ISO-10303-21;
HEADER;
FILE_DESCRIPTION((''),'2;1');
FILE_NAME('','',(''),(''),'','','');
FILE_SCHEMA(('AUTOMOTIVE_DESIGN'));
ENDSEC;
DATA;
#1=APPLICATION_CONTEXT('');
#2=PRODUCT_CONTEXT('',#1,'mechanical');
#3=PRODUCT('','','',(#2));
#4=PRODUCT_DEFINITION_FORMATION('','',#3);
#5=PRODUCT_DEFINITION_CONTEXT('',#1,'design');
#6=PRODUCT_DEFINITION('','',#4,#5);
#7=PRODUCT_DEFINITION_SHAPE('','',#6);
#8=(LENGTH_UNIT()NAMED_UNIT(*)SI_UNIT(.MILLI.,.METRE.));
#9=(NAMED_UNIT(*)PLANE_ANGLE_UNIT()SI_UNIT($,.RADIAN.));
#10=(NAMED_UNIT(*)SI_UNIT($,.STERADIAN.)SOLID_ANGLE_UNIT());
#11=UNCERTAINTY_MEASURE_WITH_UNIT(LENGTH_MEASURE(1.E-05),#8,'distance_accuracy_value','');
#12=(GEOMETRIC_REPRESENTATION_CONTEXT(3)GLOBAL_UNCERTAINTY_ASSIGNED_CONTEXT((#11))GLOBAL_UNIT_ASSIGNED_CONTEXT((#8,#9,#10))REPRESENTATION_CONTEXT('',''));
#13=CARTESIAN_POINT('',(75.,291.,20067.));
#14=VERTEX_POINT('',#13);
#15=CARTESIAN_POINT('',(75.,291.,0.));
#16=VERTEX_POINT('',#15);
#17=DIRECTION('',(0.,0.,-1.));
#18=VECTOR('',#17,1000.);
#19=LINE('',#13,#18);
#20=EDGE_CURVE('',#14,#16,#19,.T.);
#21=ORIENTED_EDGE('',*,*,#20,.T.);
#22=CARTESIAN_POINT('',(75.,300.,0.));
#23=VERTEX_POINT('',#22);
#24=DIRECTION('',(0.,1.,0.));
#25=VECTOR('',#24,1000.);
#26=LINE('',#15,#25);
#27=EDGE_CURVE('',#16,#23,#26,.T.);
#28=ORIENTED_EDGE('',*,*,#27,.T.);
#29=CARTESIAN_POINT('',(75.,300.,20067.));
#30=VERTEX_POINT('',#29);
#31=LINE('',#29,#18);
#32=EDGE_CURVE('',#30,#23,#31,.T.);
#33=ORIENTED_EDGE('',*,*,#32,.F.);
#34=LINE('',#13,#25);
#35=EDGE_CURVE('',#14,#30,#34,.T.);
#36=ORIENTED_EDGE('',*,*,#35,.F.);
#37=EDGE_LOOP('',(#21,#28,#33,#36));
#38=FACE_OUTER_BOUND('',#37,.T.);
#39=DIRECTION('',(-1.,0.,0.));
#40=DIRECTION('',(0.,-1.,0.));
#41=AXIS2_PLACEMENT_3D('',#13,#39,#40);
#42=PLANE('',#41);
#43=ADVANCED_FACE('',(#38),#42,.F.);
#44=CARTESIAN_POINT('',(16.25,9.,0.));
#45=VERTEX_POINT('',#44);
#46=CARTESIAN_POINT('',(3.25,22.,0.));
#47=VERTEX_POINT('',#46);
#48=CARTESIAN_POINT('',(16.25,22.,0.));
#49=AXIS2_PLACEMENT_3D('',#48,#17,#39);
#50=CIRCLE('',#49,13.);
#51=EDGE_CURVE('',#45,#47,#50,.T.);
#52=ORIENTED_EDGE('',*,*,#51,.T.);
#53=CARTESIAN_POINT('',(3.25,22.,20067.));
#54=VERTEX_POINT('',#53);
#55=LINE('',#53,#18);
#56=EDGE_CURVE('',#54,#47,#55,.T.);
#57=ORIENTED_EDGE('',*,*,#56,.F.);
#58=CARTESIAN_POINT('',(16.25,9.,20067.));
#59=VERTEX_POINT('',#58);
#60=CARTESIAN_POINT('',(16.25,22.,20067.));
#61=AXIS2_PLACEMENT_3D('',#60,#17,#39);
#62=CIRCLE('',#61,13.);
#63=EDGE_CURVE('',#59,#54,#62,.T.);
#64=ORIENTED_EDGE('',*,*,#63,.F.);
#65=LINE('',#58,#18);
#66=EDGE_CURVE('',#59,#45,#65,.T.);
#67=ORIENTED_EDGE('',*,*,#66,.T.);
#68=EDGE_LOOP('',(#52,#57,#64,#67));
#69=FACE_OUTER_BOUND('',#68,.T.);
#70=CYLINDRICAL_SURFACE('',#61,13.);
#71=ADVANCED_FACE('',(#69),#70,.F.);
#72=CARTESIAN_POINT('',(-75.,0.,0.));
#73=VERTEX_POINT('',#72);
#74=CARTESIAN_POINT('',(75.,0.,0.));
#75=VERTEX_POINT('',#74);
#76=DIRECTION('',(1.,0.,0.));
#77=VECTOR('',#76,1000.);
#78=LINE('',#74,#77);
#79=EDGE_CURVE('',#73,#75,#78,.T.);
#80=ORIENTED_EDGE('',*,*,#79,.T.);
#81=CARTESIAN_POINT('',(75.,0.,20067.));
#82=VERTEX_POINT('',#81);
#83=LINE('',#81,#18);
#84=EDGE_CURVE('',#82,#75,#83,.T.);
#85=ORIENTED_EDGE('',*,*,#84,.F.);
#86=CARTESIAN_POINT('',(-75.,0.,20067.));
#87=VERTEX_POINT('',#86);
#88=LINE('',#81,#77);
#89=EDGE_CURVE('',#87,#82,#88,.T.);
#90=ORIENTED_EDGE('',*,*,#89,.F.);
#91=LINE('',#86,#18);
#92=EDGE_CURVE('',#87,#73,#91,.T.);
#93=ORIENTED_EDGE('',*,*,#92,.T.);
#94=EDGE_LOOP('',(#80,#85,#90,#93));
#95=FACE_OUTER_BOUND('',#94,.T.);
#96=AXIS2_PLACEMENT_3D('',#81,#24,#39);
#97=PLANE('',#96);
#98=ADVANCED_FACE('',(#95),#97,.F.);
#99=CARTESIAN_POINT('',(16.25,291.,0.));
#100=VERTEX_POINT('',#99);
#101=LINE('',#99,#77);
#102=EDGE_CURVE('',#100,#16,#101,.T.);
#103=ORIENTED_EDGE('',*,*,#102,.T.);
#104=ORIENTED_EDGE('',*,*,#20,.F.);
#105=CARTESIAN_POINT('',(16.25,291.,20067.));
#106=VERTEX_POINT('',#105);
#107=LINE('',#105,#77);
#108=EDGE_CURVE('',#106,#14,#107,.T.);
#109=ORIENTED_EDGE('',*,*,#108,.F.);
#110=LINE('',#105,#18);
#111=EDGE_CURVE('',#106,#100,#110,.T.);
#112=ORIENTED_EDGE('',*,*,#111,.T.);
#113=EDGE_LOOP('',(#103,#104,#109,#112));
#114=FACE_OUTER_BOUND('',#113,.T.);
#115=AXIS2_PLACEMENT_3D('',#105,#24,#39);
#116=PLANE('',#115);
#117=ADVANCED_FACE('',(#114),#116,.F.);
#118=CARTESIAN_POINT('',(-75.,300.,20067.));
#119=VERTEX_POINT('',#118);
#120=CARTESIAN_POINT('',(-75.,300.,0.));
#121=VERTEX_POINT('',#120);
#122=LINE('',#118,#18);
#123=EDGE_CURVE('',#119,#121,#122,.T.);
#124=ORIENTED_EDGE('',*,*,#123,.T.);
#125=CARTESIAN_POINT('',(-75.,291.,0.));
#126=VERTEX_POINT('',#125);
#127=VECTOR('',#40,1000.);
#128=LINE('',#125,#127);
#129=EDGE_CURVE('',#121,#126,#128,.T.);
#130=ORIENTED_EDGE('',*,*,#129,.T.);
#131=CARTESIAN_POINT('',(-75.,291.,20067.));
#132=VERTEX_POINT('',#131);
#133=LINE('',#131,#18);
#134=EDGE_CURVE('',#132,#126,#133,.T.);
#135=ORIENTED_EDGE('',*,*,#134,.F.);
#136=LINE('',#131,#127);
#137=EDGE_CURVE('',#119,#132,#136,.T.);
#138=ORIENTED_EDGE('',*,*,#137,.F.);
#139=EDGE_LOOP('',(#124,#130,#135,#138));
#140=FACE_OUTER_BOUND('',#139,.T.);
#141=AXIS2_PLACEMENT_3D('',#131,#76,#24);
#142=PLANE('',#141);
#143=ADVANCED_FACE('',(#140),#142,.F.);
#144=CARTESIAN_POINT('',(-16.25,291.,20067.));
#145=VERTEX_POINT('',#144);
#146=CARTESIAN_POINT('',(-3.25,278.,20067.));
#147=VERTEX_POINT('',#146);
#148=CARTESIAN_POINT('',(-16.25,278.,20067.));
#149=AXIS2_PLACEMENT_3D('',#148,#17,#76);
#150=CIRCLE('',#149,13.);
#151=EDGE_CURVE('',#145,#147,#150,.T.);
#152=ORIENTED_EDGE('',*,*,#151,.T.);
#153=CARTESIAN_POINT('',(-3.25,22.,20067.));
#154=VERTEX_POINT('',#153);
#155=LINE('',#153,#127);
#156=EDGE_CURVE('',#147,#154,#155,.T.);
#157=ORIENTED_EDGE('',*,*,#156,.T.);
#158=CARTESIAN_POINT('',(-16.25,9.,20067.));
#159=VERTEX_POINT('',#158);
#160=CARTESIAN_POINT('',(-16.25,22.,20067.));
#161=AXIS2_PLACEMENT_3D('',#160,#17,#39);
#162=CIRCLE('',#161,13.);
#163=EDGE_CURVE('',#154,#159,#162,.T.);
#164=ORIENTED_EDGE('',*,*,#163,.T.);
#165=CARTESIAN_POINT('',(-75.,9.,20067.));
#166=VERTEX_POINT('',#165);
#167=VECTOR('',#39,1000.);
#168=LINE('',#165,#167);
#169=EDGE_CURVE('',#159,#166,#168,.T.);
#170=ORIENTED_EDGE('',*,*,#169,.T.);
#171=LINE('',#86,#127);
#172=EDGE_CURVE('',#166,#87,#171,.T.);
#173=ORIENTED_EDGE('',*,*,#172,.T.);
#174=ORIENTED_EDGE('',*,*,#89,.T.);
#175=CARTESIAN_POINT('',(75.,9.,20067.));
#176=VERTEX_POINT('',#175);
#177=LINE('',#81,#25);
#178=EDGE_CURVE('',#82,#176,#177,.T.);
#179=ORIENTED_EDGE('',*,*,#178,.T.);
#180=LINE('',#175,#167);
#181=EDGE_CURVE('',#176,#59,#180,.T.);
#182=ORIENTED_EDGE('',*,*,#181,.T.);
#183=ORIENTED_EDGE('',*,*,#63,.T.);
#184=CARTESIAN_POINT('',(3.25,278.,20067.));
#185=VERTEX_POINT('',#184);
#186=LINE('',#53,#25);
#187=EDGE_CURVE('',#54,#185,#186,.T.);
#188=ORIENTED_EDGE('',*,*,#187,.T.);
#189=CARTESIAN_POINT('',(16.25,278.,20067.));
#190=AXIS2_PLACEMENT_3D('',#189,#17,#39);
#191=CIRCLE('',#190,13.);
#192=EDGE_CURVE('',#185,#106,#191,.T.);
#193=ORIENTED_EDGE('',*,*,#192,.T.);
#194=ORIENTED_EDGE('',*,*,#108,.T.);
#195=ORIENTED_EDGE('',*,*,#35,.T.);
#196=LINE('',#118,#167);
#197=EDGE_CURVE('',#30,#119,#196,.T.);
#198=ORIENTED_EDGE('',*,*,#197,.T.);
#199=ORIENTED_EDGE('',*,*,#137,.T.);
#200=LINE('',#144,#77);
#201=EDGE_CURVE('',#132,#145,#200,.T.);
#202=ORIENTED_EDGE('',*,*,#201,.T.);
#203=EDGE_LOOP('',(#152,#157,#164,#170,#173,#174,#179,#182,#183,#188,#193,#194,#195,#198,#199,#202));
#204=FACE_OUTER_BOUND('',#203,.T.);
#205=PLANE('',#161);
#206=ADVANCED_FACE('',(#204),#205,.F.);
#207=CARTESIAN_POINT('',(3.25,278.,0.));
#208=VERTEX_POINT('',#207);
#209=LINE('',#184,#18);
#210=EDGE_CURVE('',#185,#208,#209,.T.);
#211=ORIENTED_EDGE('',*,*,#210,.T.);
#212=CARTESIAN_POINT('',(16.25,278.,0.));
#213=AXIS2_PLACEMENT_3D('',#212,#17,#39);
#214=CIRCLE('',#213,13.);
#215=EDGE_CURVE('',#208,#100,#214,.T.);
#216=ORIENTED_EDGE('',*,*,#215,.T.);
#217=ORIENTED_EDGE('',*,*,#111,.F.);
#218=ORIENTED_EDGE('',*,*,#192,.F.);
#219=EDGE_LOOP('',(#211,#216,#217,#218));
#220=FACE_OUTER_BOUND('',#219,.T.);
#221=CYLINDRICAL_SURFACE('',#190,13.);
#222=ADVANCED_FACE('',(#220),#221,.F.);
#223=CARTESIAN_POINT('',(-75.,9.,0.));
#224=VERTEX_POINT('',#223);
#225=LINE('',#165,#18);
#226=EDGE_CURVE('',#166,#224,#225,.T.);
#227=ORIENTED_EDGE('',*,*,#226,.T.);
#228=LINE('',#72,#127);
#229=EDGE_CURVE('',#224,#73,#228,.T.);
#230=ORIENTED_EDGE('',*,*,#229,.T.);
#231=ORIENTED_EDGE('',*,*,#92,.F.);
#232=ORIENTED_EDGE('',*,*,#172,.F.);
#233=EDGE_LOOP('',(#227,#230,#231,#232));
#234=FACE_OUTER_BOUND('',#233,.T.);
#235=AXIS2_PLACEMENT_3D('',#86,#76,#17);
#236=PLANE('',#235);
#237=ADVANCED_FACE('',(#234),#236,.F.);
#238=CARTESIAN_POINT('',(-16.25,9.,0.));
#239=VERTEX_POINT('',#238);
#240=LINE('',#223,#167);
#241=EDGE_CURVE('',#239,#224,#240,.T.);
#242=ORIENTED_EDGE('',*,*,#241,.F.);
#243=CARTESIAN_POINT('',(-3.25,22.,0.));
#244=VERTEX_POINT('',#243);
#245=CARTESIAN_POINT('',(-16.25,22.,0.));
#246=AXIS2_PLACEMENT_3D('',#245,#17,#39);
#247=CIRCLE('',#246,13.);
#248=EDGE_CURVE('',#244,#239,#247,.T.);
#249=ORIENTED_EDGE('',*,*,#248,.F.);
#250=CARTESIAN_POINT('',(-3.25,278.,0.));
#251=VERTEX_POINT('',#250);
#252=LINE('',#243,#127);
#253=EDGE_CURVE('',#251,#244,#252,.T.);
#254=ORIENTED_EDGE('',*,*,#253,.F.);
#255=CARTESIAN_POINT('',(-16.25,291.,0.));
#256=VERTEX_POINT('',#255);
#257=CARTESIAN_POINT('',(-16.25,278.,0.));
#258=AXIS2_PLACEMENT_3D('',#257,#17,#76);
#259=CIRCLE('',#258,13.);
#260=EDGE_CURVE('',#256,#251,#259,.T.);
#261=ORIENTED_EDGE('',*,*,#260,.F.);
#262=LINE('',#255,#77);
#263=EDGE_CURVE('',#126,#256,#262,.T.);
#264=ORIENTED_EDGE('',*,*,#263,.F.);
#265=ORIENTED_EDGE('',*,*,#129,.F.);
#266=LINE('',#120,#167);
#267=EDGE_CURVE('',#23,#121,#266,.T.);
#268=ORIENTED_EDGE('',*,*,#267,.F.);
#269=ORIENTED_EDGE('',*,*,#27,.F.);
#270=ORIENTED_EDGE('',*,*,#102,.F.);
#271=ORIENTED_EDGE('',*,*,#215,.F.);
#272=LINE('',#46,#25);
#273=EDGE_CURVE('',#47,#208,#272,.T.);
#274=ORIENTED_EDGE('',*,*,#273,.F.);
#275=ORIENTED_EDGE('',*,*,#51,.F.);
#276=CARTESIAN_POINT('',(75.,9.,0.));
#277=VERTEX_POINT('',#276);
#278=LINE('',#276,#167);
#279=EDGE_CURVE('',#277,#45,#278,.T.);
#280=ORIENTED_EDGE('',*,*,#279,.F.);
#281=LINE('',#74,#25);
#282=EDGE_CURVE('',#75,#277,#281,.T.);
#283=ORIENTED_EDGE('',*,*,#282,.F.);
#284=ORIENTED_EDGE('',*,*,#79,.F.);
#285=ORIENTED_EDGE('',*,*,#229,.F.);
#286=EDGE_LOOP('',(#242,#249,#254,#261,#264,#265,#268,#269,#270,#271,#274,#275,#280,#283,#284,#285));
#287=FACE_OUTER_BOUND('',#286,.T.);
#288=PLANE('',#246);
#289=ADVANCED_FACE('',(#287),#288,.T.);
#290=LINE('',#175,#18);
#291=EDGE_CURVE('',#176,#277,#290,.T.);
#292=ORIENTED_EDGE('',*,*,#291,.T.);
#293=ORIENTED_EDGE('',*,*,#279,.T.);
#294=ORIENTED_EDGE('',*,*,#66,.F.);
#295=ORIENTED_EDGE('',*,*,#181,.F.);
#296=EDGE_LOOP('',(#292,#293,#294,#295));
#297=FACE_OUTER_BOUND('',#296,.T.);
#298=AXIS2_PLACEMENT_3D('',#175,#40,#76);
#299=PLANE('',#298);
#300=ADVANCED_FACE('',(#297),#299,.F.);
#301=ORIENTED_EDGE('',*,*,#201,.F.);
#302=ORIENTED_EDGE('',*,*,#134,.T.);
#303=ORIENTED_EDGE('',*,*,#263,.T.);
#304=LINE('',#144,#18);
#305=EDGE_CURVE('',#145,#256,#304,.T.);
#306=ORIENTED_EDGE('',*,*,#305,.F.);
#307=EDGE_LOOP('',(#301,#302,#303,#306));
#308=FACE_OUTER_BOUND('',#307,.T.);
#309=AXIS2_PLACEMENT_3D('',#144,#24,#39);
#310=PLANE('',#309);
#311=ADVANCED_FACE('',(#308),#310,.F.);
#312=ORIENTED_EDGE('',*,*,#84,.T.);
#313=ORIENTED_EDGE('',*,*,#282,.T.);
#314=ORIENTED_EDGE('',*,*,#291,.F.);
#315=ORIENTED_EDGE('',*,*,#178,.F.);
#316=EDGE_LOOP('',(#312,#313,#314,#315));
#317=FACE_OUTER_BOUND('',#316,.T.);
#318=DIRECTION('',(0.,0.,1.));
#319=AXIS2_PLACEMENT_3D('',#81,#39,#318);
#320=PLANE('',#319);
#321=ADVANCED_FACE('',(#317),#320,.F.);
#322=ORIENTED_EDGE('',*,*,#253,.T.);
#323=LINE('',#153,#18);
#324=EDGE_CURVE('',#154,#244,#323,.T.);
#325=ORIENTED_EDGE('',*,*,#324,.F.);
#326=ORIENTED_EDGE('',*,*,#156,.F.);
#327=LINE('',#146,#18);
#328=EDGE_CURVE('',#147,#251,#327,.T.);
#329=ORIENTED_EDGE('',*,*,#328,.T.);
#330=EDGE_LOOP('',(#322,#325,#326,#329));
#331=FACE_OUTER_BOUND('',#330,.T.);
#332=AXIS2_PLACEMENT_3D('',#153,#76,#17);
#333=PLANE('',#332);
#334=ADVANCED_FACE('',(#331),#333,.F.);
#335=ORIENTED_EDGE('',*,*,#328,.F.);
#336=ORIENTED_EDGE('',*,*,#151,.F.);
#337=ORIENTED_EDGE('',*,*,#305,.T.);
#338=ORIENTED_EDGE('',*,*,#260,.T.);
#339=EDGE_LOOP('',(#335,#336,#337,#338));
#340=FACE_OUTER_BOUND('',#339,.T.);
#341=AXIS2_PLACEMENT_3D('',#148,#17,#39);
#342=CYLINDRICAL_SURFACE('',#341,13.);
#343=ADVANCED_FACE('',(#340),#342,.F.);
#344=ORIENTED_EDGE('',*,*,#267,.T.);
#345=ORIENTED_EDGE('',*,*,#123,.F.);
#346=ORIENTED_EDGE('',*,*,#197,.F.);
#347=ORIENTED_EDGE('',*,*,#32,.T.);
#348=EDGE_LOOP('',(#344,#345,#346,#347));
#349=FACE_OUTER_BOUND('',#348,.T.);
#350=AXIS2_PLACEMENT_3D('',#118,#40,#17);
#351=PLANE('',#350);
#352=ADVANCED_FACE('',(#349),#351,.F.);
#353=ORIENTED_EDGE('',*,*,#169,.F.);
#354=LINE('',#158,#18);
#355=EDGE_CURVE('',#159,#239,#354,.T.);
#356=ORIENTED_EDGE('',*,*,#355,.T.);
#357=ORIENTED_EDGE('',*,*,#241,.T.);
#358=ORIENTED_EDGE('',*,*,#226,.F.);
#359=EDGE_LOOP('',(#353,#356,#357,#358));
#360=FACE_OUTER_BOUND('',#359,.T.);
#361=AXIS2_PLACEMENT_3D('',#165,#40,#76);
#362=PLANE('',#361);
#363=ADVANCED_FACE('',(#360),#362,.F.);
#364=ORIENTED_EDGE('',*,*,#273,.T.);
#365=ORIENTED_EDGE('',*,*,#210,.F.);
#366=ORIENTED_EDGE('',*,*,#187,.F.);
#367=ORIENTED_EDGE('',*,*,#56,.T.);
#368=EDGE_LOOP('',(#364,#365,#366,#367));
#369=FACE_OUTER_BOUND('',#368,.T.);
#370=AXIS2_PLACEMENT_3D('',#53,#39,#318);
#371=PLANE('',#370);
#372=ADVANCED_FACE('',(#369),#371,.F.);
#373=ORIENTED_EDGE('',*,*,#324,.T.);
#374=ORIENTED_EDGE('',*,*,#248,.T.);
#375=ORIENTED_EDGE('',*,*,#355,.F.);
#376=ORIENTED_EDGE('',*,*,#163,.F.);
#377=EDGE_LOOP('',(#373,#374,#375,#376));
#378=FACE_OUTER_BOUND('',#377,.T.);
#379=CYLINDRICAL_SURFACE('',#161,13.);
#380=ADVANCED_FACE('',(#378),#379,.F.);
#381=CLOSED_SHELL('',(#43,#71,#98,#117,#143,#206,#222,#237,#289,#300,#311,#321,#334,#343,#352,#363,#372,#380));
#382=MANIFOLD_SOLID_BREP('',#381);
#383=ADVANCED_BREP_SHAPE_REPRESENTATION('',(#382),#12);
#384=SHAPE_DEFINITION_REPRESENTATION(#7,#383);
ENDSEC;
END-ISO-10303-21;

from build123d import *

# Parameters (mm, degrees)
BOSS_EXTRUDE1_DEPTH = 20067


with BuildPart() as part:
    # Sketch1 → Boss-Extrude1 (new body)
    with BuildSketch(Plane.XY):
        with BuildLine():
            Line((75, 0), (-75, 0))
            Line((-75, 0), (-75, 9))
            Line((-75, 9), (-16.25, 9))
            ThreePointArc((-16.25, 9), (-7.057611845, 12.807611845), (-3.25, 22))
            Line((-3.25, 22), (-3.25, 278))
            ThreePointArc((-3.25, 278), (-7.057611845, 287.192388155), (-16.25, 291))
            Line((-16.25, 291), (-75, 291))
            Line((-75, 291), (-75, 300))
            Line((-75, 300), (75, 300))
            Line((75, 300), (75, 291))
            Line((75, 291), (16.25, 291))
            ThreePointArc((16.25, 291), (7.057611845, 287.192388155), (3.25, 278))
            Line((3.25, 278), (3.25, 22))
            ThreePointArc((3.25, 22), (7.057611845, 12.807611845), (16.25, 9))
            Line((16.25, 9), (75, 9))
            Line((75, 9), (75, 0))
        make_face()
    extrude(amount=BOSS_EXTRUDE1_DEPTH)


solid = part.part
